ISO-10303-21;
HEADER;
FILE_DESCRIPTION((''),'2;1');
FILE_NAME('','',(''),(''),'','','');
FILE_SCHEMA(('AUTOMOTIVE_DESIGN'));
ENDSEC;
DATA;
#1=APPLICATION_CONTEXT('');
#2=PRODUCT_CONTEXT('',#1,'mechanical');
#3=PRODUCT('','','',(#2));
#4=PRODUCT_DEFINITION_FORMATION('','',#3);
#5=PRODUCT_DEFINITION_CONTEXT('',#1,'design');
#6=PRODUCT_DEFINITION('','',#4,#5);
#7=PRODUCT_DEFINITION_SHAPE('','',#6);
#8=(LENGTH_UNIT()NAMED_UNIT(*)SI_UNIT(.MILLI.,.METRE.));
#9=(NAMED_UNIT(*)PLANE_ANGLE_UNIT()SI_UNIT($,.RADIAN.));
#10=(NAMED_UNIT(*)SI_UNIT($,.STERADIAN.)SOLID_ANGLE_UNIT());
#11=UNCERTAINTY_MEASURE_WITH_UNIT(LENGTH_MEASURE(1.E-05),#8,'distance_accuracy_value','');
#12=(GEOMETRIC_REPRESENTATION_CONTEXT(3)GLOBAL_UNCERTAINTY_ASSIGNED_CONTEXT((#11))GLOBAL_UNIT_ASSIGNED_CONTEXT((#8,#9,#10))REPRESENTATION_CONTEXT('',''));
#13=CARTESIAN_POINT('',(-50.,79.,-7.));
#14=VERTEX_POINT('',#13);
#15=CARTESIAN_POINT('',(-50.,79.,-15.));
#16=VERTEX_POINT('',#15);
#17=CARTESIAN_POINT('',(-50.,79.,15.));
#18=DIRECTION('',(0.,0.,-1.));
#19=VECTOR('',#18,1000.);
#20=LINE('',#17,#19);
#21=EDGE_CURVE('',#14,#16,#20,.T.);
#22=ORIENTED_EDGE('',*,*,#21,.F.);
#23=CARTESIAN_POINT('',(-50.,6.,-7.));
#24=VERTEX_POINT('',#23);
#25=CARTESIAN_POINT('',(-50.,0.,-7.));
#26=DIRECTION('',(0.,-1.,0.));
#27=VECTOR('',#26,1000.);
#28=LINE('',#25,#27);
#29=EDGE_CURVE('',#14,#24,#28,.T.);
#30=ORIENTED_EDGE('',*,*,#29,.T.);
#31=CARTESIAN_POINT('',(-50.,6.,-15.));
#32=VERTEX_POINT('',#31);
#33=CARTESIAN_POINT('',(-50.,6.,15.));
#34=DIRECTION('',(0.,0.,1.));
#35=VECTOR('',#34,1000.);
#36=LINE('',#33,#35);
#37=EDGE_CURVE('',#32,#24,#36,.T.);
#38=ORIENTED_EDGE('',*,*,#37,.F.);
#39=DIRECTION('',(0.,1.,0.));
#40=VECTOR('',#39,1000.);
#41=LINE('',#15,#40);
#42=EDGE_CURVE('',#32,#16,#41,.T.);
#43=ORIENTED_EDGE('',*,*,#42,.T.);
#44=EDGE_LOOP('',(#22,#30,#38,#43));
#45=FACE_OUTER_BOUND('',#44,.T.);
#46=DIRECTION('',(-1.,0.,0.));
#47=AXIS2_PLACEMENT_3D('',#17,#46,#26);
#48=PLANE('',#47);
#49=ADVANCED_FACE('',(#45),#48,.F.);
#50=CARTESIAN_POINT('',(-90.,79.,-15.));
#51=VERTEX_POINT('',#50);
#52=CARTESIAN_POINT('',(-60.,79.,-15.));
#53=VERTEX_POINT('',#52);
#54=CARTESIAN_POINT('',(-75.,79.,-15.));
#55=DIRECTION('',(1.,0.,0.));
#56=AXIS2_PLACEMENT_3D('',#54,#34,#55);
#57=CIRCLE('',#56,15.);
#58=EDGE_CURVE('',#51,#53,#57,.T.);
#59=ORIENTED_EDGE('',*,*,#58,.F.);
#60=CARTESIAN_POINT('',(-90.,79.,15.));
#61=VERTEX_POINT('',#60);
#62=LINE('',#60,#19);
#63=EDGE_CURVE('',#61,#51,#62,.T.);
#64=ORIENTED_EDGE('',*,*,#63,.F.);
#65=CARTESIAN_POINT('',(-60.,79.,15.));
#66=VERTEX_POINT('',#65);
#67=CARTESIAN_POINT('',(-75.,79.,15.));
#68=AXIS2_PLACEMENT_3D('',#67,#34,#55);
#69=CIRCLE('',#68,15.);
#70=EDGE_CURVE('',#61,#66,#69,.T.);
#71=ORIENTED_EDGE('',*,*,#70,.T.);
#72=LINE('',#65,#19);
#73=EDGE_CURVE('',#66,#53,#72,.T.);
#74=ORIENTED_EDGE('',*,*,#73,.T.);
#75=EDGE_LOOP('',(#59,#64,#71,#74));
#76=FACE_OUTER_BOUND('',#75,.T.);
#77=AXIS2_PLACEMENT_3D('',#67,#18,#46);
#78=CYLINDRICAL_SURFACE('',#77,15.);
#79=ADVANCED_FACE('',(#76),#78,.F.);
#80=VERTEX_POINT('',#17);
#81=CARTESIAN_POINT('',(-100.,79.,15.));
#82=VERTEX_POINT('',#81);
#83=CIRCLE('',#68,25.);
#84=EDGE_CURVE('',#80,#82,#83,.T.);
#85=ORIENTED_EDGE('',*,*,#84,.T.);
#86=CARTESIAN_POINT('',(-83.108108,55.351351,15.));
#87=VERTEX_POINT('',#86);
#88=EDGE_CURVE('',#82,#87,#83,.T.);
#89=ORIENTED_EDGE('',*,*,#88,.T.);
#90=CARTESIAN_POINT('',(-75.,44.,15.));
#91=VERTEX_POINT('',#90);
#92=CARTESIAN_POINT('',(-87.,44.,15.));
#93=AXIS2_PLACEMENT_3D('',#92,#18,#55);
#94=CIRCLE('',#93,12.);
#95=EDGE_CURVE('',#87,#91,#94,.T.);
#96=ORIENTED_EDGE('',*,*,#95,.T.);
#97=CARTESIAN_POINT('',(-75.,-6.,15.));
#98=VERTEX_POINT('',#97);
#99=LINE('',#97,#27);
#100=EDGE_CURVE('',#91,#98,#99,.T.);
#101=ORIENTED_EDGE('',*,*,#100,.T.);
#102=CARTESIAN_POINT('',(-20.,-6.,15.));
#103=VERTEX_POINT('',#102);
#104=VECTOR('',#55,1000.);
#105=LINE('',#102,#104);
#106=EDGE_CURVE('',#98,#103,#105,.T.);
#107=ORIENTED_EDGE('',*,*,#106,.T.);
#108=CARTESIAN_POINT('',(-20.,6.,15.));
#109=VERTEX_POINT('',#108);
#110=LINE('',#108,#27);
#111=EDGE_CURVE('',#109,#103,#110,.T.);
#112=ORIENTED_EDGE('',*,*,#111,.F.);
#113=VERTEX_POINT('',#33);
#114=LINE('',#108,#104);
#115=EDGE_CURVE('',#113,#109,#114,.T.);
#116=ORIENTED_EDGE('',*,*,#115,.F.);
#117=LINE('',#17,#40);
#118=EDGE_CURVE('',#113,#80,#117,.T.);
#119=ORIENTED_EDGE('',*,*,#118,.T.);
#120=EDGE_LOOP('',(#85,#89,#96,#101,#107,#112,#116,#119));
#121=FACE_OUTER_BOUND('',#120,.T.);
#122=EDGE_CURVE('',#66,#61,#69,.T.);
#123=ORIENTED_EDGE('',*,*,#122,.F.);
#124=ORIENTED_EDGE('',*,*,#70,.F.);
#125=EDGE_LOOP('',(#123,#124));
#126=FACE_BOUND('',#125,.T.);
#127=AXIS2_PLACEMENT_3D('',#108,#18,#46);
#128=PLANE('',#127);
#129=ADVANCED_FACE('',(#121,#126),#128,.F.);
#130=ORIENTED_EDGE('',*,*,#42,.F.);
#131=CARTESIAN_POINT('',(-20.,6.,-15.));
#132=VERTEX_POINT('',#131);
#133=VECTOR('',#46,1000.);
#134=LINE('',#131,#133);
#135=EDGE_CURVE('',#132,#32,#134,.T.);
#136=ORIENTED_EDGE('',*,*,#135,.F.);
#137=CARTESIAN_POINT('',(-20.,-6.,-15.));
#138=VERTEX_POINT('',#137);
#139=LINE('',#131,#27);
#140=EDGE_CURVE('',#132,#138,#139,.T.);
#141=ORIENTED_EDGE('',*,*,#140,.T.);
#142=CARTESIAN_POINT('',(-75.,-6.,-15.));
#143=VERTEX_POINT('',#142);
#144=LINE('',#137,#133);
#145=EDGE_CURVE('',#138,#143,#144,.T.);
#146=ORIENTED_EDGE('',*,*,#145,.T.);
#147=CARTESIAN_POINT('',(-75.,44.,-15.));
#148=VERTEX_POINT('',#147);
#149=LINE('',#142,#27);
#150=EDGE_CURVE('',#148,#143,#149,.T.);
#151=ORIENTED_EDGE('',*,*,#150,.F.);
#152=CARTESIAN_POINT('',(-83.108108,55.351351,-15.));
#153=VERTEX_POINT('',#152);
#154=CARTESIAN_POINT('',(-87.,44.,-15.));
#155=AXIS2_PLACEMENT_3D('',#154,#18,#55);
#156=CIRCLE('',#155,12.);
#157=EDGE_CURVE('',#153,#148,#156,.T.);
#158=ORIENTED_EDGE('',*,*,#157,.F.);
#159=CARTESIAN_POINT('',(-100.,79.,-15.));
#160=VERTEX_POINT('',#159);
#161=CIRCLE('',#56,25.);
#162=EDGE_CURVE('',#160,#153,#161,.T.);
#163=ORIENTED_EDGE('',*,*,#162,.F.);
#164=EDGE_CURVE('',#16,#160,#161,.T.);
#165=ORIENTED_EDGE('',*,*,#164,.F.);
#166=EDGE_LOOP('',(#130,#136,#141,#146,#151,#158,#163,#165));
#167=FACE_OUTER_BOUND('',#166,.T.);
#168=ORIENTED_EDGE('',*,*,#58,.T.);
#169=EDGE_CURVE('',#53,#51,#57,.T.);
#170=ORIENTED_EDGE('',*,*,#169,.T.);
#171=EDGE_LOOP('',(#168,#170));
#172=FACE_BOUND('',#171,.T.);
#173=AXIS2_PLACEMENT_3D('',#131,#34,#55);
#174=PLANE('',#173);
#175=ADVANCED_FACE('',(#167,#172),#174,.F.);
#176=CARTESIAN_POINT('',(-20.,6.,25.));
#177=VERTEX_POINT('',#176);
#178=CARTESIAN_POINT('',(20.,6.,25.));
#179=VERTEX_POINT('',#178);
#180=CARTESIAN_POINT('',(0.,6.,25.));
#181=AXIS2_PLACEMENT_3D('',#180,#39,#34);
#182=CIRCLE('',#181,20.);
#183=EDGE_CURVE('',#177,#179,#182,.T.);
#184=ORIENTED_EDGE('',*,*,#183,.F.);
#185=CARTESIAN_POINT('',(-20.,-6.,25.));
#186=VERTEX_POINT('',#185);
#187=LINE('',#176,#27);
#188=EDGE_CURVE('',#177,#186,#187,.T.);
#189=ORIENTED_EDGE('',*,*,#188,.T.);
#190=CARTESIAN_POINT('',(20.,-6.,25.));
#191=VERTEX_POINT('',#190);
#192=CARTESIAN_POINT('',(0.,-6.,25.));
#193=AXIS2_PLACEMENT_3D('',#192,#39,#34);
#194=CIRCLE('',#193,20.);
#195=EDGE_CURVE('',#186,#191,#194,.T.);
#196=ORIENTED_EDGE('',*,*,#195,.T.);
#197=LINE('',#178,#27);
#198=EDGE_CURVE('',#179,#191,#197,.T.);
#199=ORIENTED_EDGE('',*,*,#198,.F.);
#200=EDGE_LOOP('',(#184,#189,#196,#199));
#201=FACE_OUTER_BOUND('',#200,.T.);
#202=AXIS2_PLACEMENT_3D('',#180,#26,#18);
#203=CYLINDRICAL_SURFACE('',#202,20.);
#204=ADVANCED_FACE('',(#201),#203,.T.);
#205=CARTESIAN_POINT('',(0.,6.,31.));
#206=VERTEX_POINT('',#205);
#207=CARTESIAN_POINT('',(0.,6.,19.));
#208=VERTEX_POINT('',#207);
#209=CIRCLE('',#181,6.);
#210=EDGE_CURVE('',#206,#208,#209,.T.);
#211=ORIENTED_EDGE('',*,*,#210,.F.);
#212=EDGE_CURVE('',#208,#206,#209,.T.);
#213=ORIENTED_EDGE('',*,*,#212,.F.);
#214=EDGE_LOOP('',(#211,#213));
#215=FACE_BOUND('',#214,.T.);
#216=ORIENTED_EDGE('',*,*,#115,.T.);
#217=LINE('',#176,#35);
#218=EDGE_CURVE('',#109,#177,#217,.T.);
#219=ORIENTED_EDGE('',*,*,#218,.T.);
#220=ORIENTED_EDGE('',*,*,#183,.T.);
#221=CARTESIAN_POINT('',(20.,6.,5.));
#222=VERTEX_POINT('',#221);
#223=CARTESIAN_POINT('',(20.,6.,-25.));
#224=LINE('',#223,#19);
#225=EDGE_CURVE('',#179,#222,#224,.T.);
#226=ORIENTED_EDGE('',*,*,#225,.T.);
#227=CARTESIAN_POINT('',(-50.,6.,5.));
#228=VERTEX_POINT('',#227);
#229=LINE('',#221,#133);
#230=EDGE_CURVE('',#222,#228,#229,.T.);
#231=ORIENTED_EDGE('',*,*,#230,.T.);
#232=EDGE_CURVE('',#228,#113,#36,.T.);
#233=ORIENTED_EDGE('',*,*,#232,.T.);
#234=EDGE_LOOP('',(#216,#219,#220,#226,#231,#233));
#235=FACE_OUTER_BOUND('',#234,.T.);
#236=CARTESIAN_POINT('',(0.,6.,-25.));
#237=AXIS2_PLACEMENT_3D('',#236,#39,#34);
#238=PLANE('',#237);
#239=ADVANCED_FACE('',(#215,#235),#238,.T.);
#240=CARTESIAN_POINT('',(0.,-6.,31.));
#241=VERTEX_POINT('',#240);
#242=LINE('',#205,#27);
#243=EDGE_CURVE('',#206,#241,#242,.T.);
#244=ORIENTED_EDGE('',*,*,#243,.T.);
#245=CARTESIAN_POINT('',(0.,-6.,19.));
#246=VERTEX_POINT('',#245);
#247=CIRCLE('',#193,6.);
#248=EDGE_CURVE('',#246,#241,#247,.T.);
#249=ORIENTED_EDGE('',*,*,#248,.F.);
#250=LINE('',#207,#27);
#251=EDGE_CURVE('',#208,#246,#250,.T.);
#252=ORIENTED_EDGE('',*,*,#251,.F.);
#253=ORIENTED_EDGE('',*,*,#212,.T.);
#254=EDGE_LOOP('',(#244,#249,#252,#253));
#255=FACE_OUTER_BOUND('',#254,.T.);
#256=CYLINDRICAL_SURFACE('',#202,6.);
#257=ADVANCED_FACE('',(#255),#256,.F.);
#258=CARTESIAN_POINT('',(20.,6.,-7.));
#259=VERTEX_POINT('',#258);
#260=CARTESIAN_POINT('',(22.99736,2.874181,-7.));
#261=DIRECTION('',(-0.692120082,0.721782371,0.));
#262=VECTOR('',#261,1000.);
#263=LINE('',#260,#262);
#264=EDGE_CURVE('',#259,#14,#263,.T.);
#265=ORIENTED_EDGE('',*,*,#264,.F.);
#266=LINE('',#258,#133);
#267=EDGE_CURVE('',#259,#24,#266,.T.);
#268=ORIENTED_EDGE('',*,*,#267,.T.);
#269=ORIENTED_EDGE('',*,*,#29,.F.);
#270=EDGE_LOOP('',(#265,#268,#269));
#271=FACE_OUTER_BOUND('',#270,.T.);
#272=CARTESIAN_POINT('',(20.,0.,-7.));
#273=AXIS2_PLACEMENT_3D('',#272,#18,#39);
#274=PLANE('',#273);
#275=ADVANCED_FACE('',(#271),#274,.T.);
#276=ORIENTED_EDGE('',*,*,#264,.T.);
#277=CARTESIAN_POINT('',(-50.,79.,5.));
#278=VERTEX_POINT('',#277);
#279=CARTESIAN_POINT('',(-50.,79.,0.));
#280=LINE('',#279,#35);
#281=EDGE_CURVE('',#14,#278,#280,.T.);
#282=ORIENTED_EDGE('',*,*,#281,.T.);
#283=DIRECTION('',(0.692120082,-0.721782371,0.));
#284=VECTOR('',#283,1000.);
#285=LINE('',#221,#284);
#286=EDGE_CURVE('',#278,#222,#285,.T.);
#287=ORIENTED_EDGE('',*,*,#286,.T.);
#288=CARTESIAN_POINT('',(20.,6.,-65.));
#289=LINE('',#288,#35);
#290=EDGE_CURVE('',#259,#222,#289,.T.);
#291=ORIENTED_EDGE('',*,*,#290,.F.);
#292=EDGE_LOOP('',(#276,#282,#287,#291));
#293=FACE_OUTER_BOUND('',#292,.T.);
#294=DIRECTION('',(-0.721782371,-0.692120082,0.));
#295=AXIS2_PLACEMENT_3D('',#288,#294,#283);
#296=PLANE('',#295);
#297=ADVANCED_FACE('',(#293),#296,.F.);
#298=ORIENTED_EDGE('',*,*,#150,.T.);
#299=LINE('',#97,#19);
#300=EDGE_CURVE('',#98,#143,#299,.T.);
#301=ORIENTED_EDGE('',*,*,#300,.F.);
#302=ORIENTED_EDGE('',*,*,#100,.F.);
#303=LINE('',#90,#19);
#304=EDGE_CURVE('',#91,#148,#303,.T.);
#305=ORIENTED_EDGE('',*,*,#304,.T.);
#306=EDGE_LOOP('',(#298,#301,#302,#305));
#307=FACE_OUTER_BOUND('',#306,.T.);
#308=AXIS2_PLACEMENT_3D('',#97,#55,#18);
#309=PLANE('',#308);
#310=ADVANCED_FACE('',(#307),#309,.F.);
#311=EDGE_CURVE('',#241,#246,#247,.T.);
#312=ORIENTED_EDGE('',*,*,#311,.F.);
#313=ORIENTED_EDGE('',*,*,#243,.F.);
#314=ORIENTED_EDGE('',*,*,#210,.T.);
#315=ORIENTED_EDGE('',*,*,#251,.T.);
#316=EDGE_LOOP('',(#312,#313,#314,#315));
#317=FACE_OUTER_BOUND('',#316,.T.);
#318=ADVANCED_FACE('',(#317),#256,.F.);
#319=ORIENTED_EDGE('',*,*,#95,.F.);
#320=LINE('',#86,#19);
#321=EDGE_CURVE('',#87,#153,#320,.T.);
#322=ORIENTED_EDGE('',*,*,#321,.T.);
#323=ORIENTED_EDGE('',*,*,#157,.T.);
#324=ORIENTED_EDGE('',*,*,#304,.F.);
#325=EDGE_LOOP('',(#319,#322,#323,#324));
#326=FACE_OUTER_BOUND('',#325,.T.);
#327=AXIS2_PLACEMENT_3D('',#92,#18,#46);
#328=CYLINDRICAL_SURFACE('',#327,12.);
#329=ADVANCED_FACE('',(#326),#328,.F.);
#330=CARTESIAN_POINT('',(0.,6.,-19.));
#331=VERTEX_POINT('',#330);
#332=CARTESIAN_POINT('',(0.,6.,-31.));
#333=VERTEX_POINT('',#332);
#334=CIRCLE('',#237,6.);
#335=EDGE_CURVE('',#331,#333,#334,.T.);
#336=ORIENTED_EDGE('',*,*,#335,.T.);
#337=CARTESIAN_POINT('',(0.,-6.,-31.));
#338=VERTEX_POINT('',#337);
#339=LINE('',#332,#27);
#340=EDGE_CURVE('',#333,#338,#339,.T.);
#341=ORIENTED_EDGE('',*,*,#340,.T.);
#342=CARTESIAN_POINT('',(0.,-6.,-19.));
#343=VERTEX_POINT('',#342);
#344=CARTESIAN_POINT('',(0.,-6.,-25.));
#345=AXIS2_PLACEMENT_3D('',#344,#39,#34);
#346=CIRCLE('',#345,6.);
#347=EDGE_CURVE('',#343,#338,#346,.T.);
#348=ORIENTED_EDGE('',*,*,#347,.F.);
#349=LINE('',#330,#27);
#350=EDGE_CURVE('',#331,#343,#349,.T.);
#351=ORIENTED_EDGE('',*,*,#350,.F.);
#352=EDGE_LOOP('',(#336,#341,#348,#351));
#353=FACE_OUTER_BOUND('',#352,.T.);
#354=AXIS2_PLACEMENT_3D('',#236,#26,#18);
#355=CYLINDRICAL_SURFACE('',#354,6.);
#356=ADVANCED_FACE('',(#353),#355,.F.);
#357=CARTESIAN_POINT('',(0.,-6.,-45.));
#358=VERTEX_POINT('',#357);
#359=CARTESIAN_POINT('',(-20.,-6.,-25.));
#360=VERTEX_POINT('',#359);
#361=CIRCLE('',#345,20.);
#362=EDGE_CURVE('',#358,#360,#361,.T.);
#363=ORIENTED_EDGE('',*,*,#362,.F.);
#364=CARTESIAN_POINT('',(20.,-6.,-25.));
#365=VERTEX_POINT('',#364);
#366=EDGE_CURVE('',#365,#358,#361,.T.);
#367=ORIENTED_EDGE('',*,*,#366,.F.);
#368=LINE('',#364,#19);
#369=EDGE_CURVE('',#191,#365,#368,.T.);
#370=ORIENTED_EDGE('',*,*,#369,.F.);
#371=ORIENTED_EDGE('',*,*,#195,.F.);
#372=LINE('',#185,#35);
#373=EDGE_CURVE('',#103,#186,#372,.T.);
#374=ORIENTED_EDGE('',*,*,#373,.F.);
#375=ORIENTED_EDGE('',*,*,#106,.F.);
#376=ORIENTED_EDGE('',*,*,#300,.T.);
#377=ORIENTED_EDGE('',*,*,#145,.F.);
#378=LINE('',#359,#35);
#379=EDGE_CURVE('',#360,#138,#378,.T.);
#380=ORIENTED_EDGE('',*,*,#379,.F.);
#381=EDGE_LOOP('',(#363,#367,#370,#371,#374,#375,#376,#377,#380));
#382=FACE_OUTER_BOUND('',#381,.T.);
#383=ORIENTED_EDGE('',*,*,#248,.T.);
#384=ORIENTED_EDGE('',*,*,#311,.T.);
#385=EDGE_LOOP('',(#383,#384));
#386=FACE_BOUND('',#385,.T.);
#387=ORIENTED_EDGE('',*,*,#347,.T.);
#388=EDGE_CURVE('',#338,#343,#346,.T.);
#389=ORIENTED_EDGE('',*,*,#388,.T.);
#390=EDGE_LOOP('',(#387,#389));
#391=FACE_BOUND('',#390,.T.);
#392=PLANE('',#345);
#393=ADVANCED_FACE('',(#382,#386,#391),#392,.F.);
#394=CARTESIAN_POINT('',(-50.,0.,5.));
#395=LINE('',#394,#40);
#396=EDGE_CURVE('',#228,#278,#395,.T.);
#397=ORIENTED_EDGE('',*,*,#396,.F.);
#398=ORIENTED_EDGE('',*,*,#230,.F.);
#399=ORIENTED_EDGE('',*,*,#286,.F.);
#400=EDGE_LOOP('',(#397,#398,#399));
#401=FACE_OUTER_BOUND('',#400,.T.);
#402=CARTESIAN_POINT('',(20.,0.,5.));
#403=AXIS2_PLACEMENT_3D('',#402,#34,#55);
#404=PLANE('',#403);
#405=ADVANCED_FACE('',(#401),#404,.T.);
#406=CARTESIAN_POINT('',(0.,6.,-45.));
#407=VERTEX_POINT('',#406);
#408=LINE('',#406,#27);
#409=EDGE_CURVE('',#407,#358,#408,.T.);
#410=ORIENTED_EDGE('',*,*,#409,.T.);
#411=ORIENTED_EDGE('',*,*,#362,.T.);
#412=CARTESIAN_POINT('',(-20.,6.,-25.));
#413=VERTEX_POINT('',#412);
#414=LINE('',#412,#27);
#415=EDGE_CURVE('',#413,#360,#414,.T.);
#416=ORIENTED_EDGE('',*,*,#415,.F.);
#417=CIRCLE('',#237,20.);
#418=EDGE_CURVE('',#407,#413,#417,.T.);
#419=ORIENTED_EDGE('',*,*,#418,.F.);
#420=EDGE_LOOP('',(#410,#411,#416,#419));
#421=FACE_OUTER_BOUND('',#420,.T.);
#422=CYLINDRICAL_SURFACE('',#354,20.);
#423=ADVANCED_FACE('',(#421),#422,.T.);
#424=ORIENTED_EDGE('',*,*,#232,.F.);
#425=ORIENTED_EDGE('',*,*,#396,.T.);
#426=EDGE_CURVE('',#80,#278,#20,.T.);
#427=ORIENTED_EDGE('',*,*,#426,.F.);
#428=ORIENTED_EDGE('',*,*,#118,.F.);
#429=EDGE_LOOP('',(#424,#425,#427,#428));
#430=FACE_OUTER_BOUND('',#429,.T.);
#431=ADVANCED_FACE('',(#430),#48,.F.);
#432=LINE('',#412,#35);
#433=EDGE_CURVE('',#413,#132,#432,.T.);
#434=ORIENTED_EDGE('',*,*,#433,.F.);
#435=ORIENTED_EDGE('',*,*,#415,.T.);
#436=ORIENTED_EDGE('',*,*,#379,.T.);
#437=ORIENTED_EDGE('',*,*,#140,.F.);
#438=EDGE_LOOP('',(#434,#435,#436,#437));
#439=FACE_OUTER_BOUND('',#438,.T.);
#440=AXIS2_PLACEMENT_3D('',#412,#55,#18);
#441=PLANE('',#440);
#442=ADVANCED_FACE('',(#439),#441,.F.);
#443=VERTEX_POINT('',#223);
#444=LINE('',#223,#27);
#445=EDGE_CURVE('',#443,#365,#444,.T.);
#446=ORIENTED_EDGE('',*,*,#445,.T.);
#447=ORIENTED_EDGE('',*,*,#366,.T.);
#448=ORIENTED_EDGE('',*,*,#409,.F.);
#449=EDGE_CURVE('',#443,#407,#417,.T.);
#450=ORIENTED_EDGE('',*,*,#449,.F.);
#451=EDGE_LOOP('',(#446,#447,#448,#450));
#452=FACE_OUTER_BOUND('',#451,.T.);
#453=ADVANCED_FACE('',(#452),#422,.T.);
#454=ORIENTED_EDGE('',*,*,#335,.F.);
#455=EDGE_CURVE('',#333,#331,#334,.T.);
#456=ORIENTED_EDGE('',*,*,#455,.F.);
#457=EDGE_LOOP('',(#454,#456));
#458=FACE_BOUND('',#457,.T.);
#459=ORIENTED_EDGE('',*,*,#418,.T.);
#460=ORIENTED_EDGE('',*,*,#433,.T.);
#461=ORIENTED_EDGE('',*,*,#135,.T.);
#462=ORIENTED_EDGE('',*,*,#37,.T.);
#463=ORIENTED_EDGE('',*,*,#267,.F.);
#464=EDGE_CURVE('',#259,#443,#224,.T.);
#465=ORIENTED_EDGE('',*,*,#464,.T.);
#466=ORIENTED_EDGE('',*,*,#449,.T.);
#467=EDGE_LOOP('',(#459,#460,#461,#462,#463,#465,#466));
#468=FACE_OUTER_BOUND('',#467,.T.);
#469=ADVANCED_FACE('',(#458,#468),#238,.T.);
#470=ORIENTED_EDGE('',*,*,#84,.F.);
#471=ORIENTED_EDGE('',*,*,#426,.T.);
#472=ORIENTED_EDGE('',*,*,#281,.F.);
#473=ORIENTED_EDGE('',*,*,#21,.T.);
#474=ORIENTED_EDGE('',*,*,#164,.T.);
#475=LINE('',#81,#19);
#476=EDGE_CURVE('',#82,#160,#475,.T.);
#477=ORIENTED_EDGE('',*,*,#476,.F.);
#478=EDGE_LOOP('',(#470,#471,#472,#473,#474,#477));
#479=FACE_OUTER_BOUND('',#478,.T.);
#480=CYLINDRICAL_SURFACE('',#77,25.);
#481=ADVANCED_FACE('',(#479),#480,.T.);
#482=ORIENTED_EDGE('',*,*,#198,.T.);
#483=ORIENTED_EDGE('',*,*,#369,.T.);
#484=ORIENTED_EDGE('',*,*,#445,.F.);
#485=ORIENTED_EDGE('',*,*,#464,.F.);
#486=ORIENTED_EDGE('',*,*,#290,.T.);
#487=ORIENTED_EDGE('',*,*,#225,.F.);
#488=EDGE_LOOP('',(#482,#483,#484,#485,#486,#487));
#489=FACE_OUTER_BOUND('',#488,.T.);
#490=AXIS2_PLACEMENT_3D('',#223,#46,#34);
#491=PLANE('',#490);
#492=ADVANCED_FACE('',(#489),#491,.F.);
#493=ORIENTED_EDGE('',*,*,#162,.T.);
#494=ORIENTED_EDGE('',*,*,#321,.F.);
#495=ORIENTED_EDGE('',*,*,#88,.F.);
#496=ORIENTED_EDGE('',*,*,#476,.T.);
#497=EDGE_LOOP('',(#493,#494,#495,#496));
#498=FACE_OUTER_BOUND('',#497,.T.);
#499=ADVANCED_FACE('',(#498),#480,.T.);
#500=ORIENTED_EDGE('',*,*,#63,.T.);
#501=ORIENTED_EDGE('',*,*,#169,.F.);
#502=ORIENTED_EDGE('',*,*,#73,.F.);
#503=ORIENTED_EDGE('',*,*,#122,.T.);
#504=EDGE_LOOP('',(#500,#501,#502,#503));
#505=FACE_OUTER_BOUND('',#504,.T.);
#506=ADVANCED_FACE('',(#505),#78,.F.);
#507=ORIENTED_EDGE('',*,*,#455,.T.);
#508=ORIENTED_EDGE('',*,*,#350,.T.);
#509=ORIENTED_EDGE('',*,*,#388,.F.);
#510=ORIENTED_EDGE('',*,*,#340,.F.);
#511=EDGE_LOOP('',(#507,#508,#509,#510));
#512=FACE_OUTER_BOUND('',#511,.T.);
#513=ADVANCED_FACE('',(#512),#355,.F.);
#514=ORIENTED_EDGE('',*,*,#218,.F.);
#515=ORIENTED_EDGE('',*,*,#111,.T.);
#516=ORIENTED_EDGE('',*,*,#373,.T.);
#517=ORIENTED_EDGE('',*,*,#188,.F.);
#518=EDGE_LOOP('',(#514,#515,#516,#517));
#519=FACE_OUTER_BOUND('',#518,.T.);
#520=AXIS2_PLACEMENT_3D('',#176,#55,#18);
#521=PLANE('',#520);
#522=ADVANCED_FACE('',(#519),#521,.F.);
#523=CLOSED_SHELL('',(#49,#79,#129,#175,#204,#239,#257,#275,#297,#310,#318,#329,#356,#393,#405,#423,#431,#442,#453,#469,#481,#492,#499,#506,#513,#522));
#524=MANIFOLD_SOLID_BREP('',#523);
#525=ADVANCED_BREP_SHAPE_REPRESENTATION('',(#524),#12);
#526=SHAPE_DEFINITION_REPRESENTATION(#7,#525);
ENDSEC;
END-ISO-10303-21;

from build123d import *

# Parameters (mm, degrees)
BASE_PLATE_SKETCH_R     = 6
BASE_PLATE_DEPTH        = 6
UPRIGHT_BORE_SKETCH_R   = 15
UPRIGHT_WITH_BORE_DEPTH = 15
RIB_SKETCH_W            = 12
RIB_SKETCH_H            = 73
RIB_DEPTH               = 70
RIB_WEDGE_CUT_DEPTH     = 70


with BuildPart() as part:
    # Base Plate Sketch → Base Plate (new, symmetric)
    with BuildSketch(Plane(origin=(0, 0, 0), x_dir=(1, 0, 0), z_dir=(0, 1, 0))):
        with BuildLine():
            Line((-20, 25), (-20, 15))
            Line((-20, 15), (-50, 15))
            Line((-50, 15), (-50, -15))
            Line((-50, -15), (-20, -15))
            Line((-20, -15), (-20, -25))
            ThreePointArc((-20, -25), (0, -45), (20, -25))
            Line((20, -25), (20, 25))
            ThreePointArc((20, 25), (0, 45), (-20, 25))
        make_face()
        with Locations(Location((0, 25, 0), (0, 0, 270))):
            Circle(BASE_PLATE_SKETCH_R, mode=Mode.SUBTRACT)
        with Locations(Location((0, -25, 0), (0, 0, 270))):
            Circle(BASE_PLATE_SKETCH_R, mode=Mode.SUBTRACT)
    extrude(amount=BASE_PLATE_DEPTH, both=True)

    # Upright Bore Sketch → Upright with Bore (add, symmetric)
    with BuildSketch(Plane.XY):
        with BuildLine():
            Line((-50, -6), (-75, -6))
            Line((-75, -6), (-75, 44))
            ThreePointArc((-75, 44), (-77.235198346, 50.974858325), (-83.108108108, 55.351351351))
            ThreePointArc((-83.108108108, 55.351351351), (-89.530954843, 99.34333678), (-50, 79))
            Line((-50, 79), (-50, -6))
        make_face()
        with Locations((-75, 79)):
            Circle(UPRIGHT_BORE_SKETCH_R, mode=Mode.SUBTRACT)
    extrude(amount=UPRIGHT_WITH_BORE_DEPTH, both=True)

    # Rib Sketch → Rib (add)
    with BuildSketch(Plane(origin=(-50, 0, 0), x_dir=(0, 0, -1), z_dir=(1, 0, 0))):
        with Locations((1, 42.5)):
            Rectangle(RIB_SKETCH_W, RIB_SKETCH_H)
    extrude(amount=RIB_DEPTH)

    # Rib Wedge Cut Sketch → Rib Wedge Cut (cut)
    with BuildSketch(Plane.XY.offset(5)):
        Polygon((20, 6), (-50, 79), (20, 79), align=None)
    extrude(amount=-RIB_WEDGE_CUT_DEPTH, mode=Mode.SUBTRACT)


solid = part.part
